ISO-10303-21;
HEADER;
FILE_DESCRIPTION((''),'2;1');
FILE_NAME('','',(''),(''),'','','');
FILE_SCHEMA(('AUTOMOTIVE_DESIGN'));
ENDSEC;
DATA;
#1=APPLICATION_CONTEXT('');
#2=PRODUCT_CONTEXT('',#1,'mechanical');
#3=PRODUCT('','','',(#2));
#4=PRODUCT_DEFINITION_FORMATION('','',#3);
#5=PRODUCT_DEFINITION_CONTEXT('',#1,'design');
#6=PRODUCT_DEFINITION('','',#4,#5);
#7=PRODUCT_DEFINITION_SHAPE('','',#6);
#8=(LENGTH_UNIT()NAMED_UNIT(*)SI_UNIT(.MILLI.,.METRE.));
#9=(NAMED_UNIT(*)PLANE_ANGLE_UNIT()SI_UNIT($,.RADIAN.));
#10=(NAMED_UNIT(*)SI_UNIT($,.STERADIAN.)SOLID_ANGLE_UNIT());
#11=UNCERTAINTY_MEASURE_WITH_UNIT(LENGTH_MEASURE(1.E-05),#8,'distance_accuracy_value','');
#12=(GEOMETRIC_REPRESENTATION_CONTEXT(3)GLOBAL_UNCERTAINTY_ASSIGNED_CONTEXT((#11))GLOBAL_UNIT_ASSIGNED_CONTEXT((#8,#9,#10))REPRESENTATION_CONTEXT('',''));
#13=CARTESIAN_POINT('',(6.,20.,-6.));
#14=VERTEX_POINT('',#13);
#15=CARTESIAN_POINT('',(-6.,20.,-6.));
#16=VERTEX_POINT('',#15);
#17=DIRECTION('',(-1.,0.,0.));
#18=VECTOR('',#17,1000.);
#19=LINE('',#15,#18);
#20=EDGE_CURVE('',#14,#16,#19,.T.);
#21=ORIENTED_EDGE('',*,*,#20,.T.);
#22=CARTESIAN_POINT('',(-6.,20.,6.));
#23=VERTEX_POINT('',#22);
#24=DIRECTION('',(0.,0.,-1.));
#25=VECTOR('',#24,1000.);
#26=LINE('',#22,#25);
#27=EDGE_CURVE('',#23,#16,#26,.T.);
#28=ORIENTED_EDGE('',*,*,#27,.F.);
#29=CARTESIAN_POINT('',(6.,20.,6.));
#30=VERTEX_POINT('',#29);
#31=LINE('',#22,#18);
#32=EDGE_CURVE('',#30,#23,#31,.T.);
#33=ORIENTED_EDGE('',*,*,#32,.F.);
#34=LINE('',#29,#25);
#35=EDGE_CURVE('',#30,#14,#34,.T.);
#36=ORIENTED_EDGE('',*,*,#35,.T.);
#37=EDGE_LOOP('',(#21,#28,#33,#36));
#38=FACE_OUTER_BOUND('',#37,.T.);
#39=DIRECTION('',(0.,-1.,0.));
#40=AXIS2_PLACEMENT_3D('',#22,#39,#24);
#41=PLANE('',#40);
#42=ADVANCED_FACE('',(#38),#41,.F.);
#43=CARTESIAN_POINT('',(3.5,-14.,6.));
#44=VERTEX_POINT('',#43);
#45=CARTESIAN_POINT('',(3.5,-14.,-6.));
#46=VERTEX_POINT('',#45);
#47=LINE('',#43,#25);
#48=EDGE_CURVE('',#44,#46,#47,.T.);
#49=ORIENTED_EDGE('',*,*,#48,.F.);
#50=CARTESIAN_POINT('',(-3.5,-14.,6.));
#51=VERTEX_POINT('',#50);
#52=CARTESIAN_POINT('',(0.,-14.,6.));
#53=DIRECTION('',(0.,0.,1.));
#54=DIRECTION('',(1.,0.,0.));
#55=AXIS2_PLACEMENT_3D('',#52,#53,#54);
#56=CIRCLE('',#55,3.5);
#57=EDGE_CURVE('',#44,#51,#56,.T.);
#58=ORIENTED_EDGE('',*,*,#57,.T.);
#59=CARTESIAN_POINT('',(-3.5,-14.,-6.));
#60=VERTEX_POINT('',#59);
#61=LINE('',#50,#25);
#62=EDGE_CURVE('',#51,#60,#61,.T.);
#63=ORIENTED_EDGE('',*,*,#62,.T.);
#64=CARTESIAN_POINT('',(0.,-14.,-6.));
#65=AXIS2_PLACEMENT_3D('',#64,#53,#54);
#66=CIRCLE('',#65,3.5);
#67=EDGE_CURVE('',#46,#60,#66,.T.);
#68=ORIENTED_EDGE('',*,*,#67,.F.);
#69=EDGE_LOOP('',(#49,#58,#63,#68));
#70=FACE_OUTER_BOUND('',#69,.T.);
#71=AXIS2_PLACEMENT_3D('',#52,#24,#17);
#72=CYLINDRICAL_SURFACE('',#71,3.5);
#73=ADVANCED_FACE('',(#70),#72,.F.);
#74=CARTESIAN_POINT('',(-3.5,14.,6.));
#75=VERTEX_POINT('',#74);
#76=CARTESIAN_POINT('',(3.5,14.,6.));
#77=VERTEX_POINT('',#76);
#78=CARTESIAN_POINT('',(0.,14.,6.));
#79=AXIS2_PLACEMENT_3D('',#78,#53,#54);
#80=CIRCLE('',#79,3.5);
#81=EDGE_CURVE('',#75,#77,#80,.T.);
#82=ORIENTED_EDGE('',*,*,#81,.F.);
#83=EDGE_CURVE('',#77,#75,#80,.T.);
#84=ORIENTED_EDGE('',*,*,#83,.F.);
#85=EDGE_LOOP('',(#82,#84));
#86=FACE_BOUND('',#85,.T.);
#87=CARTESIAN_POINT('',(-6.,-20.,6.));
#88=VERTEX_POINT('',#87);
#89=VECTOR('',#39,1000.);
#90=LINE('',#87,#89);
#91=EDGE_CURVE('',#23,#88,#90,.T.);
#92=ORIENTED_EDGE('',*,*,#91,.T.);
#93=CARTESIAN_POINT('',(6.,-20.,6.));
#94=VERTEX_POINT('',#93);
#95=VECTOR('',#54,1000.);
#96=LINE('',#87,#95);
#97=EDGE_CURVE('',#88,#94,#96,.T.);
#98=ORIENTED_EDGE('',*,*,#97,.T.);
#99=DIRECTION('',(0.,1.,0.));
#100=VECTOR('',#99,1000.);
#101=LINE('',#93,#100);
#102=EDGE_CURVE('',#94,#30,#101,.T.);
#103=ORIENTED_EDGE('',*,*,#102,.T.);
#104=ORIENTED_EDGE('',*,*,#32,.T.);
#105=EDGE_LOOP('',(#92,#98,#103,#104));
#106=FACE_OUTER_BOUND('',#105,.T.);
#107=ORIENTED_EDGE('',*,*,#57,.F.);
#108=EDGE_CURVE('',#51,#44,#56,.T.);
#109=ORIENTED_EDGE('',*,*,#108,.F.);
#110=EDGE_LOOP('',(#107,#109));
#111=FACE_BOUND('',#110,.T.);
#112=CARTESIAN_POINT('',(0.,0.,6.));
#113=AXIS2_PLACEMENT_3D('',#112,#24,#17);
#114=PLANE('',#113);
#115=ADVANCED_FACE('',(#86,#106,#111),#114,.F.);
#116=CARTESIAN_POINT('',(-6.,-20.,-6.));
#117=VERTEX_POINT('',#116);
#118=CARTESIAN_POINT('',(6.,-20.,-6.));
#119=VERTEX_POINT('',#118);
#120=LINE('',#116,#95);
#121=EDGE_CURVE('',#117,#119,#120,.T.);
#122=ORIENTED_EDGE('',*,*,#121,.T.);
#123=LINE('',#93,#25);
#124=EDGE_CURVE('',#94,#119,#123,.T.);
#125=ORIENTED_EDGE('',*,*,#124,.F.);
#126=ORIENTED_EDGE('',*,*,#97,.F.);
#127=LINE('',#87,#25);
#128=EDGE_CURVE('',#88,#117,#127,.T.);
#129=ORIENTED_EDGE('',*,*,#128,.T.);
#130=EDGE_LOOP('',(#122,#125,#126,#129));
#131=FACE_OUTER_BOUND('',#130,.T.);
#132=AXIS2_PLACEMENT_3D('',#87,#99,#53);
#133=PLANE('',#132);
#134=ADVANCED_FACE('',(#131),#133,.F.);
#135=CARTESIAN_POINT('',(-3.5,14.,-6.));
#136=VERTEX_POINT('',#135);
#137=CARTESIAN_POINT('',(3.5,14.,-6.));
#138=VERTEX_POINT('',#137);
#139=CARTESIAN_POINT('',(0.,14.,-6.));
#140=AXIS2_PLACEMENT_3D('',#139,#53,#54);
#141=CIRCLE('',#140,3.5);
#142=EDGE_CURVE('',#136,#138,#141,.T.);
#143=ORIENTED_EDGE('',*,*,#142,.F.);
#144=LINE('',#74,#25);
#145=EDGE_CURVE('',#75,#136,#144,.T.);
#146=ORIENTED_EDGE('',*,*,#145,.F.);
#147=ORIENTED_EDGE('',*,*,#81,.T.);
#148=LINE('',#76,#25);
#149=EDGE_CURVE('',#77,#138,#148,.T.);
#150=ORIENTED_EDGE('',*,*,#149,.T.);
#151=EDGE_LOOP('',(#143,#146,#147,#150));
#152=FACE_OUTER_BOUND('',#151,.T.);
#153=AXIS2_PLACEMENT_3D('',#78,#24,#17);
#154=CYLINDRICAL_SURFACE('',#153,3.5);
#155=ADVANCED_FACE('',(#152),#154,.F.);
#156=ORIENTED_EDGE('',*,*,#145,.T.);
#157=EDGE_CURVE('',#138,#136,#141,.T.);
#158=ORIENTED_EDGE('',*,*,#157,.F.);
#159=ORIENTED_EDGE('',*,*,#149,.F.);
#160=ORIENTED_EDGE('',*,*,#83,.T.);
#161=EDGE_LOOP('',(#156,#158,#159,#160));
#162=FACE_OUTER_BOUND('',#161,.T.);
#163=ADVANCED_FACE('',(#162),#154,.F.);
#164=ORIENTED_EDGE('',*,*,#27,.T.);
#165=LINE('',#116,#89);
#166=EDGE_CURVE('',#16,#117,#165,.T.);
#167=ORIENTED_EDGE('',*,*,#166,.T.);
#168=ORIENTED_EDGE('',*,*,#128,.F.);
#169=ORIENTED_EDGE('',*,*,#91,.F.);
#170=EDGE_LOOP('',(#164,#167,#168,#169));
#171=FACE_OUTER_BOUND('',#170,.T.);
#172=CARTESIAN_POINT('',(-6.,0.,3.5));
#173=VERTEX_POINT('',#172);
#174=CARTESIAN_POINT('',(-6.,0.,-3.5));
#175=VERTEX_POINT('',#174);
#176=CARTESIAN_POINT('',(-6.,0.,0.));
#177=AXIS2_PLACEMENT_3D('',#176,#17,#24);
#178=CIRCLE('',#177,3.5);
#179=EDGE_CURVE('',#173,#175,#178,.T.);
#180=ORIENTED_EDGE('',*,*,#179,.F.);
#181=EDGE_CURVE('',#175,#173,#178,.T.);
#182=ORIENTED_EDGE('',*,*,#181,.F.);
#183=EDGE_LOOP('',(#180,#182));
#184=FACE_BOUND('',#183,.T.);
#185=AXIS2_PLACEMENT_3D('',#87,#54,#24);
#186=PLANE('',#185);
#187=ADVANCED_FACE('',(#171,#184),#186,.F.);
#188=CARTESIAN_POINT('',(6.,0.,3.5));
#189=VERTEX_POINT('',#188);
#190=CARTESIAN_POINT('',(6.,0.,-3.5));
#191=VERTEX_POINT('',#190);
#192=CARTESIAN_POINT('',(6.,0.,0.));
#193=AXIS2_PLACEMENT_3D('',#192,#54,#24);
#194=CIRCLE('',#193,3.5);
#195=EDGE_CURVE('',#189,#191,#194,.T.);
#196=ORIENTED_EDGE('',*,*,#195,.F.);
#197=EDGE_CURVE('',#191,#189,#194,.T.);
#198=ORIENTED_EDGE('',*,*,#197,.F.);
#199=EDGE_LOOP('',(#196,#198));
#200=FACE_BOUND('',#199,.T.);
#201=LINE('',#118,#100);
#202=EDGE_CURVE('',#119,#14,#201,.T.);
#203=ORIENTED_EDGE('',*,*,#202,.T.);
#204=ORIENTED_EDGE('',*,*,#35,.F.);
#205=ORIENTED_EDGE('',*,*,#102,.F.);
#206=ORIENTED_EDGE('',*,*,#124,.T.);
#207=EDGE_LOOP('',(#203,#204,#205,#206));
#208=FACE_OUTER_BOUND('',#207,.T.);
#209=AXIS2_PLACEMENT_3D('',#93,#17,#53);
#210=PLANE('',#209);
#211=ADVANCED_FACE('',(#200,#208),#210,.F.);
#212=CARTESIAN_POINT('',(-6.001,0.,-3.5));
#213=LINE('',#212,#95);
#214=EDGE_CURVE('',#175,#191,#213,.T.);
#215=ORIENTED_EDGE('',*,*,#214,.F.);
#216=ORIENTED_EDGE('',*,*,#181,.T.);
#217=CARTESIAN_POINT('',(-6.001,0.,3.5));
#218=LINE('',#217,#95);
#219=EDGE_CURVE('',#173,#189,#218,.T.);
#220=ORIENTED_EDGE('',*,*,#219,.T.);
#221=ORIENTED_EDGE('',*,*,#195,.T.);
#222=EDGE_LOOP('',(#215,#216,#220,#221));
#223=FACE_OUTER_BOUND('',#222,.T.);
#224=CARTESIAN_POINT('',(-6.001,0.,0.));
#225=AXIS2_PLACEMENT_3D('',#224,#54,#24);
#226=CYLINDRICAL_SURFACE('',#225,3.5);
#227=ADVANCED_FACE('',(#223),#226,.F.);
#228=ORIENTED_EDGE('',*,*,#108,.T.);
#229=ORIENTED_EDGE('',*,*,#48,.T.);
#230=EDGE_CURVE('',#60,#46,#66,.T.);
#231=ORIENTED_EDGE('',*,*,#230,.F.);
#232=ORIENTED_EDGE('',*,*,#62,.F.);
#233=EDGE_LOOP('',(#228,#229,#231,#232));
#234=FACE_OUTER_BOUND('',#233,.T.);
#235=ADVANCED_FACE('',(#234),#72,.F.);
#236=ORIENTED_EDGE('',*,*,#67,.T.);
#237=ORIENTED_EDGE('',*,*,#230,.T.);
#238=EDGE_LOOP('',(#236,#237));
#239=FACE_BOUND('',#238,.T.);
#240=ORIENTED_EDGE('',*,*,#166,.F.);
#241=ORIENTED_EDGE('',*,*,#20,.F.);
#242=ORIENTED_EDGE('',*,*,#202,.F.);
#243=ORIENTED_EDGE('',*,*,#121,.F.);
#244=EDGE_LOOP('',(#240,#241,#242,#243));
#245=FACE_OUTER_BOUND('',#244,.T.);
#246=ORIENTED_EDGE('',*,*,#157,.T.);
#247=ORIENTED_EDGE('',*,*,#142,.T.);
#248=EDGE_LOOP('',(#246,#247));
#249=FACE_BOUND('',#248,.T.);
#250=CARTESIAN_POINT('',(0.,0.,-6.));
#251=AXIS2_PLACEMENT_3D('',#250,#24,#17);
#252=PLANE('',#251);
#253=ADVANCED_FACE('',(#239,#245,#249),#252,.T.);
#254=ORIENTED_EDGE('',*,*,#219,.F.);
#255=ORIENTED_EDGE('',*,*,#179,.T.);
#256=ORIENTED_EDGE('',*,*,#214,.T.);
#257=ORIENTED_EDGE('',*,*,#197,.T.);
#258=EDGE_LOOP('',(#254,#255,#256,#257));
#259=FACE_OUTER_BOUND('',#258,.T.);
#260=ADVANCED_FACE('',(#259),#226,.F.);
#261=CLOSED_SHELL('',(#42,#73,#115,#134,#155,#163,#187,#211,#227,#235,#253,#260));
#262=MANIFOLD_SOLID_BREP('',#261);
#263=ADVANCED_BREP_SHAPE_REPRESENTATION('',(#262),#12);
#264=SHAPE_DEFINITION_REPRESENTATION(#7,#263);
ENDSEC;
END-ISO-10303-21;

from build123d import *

# Parameters (mm, degrees)
SKETCH_1_W          = 12
SKETCH_1_H          = 40
SKETCH_1_R          = 3.5
EXTRUDE_1_DEPTH     = 6
CUT_EXTRUDE_1_REACH = 26.083
SKETCH_2_R          = 3.5


with BuildPart() as part:
    # 草图1 → 凸台-拉伸1 (new, symmetric)
    with BuildSketch(Plane.XY):
        Rectangle(SKETCH_1_W, SKETCH_1_H)
        with Locations((0, 14)):
            Circle(SKETCH_1_R, mode=Mode.SUBTRACT)
        with Locations((0, -14)):
            Circle(SKETCH_1_R, mode=Mode.SUBTRACT)
    extrude(amount=EXTRUDE_1_DEPTH, both=True)

    # 草图2 → 切除-拉伸1 (cut, up to next)
    with BuildSketch(Plane(origin=(6, 0, 0), x_dir=(0, 0, -1), z_dir=(1, 0, 0)), mode=Mode.PRIVATE) as cut_extrude_1_sk1:
        Circle(SKETCH_2_R)
    cut_extrude_1_tool1 = extrude(cut_extrude_1_sk1.sketch, amount=-CUT_EXTRUDE_1_REACH, mode=Mode.PRIVATE) & part.part
    add(cut_extrude_1_tool1.solids().sort_by_distance((6, 0, 0))[0], mode=Mode.SUBTRACT)


solid = part.part
